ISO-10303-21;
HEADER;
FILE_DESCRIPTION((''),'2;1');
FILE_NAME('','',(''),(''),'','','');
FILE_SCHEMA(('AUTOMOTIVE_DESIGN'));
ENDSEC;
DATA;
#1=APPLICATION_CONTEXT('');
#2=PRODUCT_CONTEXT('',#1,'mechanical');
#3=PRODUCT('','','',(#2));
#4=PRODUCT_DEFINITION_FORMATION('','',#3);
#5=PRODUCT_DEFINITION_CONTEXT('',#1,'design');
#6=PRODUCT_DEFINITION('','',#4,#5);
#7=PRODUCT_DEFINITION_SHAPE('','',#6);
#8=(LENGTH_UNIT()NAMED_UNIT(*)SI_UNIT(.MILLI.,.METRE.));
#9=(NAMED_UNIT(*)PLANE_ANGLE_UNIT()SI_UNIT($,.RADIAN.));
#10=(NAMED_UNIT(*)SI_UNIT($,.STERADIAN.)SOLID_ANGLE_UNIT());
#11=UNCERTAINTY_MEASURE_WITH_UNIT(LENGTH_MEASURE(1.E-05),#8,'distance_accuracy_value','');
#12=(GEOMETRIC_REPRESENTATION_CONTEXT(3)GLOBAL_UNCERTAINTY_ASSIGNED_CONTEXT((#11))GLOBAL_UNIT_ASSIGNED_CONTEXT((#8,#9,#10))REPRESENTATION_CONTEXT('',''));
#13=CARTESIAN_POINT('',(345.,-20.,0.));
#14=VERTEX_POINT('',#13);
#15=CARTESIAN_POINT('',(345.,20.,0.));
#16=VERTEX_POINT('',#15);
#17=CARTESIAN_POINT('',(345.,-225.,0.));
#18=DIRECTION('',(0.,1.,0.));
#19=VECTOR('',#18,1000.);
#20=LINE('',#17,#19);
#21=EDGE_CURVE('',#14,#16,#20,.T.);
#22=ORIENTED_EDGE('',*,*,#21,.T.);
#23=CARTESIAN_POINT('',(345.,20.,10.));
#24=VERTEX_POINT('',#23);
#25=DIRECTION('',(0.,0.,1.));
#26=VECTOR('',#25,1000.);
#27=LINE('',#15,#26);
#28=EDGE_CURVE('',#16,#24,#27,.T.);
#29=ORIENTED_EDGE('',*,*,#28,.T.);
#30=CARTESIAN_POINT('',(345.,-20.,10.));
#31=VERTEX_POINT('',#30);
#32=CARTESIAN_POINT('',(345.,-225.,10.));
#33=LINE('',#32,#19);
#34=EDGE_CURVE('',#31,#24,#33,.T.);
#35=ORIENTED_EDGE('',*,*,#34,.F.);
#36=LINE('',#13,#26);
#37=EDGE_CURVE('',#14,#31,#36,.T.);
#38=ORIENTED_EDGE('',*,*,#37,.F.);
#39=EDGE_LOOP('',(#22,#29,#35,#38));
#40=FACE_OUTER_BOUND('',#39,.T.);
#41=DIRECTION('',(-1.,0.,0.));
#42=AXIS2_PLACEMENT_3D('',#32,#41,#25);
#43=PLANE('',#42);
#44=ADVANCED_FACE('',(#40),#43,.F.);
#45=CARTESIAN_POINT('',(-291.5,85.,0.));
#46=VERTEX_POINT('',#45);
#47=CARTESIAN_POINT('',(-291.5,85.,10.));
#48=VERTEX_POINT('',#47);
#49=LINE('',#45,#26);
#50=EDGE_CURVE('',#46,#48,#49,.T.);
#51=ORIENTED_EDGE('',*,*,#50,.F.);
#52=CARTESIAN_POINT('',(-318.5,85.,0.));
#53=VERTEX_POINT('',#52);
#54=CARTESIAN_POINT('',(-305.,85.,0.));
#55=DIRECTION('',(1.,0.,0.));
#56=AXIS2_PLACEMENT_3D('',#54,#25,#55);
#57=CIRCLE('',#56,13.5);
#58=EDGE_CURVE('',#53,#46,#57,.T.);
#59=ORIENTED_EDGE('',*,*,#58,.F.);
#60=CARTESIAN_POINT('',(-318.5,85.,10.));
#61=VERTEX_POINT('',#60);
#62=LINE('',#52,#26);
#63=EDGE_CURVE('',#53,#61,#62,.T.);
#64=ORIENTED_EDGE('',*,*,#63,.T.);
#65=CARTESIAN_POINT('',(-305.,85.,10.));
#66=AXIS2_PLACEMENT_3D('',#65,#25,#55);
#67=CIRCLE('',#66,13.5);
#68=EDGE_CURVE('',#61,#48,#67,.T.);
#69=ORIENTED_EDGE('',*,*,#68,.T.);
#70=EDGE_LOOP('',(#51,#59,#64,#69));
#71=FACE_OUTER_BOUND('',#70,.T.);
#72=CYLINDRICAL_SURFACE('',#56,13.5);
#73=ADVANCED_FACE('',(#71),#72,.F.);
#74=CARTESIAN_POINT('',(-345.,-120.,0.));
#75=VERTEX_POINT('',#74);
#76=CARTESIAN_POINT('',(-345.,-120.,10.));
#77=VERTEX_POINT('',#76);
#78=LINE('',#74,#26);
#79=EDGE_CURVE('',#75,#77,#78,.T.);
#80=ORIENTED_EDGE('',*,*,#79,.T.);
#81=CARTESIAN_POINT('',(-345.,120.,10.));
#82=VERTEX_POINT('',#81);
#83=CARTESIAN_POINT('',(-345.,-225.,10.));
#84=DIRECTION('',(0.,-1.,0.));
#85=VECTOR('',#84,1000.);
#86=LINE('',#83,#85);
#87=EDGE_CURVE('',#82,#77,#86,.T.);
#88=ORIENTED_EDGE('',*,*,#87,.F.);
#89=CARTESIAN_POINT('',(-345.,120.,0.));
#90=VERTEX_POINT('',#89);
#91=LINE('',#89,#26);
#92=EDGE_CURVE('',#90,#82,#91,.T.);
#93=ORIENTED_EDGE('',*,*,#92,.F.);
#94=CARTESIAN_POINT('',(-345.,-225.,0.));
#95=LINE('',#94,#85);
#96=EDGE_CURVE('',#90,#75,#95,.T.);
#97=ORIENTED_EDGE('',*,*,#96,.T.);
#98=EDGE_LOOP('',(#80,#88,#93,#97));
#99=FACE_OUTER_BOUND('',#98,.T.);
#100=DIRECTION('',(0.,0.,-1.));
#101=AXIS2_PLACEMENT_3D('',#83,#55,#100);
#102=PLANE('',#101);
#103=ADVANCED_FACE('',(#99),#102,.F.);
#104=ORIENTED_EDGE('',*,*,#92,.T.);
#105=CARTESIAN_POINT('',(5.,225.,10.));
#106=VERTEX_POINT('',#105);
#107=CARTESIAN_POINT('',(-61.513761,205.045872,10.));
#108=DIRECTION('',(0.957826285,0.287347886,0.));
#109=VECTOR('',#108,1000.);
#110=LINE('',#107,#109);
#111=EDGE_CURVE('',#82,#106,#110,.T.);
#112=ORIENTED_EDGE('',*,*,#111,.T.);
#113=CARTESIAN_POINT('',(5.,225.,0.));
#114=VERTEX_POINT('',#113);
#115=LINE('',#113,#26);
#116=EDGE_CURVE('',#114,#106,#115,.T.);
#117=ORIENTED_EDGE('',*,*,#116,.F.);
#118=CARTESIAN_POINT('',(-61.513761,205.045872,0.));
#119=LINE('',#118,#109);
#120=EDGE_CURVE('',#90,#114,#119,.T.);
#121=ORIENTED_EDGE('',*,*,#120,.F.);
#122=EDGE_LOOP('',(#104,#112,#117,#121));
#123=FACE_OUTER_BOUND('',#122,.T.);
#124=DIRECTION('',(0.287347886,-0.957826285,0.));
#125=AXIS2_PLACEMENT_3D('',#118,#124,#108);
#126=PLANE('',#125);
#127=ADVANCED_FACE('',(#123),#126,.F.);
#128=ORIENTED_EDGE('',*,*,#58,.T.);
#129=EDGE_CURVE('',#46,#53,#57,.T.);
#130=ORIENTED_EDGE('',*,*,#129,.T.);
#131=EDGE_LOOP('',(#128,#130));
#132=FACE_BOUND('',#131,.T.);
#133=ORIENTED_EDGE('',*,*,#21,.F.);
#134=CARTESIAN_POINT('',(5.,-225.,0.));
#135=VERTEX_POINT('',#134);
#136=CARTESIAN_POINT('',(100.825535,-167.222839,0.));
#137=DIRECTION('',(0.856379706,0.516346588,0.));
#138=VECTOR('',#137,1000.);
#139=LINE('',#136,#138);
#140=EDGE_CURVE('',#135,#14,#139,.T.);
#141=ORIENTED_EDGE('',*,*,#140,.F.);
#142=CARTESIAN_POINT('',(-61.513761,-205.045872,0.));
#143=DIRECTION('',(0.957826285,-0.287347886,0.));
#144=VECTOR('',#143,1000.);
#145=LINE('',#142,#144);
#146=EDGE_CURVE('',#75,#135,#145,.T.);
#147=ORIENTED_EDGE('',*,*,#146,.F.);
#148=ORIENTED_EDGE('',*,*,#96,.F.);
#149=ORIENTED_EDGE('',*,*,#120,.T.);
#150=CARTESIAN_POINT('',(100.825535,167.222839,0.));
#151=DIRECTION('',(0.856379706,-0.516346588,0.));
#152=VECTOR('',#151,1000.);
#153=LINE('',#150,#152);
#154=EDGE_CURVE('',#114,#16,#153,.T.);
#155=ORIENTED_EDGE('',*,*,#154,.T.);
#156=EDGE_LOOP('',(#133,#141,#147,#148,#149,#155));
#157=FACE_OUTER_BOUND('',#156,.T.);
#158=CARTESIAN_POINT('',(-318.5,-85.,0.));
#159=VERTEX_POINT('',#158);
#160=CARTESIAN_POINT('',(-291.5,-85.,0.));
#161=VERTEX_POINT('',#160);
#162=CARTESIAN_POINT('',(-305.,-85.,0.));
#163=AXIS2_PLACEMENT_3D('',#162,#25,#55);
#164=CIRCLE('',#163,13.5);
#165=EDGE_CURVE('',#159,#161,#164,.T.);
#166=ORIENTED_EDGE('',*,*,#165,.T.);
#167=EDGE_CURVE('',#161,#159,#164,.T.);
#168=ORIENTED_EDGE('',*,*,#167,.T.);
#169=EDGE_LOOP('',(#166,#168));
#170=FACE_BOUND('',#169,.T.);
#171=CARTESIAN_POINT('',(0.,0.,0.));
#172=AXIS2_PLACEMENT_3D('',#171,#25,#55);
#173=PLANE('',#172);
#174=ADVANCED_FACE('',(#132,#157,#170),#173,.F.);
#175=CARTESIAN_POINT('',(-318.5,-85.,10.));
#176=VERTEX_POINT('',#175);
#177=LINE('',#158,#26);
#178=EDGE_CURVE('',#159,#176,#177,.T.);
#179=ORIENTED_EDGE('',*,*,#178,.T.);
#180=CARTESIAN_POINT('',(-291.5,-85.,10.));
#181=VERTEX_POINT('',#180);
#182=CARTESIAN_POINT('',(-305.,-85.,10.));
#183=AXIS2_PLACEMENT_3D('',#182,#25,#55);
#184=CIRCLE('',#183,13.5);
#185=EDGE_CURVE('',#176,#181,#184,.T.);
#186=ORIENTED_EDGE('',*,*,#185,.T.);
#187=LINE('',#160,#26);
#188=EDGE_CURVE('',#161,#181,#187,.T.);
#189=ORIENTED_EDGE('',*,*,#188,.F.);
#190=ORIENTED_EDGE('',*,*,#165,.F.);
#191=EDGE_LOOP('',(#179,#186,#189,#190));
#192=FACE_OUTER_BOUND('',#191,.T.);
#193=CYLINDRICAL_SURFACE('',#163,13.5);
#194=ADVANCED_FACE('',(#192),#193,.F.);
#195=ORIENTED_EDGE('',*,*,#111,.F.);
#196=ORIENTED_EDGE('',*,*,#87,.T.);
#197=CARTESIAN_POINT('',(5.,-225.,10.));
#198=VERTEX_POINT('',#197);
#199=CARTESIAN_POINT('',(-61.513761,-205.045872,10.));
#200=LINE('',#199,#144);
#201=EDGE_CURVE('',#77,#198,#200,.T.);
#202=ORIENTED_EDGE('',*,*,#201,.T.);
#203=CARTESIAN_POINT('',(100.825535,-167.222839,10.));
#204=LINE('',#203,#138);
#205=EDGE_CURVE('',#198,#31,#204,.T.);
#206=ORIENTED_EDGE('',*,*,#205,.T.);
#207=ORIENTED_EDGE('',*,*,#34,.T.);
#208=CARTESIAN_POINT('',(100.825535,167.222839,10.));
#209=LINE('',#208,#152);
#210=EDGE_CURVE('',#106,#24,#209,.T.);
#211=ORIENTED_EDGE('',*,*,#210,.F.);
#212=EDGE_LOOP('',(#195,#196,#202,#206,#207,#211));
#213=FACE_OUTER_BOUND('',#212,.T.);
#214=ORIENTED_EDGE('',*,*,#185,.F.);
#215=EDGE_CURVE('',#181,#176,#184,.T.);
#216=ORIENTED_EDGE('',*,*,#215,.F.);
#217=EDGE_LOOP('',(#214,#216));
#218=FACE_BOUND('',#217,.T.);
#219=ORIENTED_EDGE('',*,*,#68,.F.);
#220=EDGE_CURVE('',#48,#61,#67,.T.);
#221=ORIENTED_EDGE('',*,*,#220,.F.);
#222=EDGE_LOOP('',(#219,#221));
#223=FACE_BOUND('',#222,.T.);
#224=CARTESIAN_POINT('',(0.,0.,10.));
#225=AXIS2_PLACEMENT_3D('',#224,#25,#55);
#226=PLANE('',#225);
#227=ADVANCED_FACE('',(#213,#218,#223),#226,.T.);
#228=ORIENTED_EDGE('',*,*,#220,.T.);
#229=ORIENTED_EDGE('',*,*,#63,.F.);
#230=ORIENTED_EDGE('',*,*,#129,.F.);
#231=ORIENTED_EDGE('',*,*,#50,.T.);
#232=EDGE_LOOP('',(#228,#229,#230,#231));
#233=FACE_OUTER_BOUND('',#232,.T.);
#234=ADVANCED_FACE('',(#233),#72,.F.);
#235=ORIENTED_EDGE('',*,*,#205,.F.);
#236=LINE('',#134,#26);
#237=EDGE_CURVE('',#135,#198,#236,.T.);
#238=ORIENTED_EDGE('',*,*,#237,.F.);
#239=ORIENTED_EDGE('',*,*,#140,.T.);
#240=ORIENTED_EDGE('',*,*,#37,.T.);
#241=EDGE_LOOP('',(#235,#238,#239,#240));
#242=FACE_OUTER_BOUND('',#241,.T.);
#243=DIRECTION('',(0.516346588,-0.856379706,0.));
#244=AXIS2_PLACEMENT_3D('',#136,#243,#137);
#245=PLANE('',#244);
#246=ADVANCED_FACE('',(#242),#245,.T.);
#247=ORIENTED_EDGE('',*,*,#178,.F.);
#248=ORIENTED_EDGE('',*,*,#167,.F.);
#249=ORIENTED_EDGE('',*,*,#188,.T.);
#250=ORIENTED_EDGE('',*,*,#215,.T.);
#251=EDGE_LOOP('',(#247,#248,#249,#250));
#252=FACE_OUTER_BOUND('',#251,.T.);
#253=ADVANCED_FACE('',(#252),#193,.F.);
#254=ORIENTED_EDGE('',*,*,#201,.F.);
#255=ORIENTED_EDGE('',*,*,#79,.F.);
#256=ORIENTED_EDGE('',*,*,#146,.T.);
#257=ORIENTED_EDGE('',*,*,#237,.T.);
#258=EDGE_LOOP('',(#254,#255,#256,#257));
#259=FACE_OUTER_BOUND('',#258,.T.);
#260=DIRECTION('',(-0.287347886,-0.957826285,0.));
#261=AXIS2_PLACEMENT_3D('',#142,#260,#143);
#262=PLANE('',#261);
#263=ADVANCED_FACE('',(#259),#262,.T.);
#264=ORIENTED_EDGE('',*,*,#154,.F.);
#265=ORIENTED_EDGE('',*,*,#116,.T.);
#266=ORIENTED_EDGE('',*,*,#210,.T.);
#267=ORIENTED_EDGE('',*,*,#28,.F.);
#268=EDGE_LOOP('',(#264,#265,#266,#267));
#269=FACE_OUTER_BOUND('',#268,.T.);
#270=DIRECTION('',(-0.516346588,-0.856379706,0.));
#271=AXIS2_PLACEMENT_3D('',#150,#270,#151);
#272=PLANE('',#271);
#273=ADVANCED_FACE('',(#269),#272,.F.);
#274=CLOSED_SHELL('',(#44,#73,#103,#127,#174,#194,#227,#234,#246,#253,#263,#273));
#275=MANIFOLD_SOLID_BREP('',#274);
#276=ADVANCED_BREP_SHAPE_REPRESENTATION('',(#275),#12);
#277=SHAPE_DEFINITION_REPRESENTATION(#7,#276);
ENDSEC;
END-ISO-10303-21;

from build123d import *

# Parameters (mm, degrees)
SKETCH_1_W          = 690
SKETCH_1_H          = 450
EXTRUDE_1_DEPTH     = 10
SKETCH_2_R          = 13.5
CUT_EXTRUDE_1_DEPTH = 10


with BuildPart() as part:
    # 草图1 → 凸台-拉伸1 (new body)
    with BuildSketch(Plane.XY):
        Rectangle(SKETCH_1_W, SKETCH_1_H)
    extrude(amount=EXTRUDE_1_DEPTH)

    # 草图2 → 切除-拉伸1 (cut)
    with BuildSketch(Plane.XY.offset(10)):
        Polygon((-345, 225), (-345, 120), (5, 225), align=None)
        Polygon((345, 225), (5, 225), (345, 20), align=None)
        Polygon((345, -20), (5, -225), (345, -225), align=None)
        Polygon((5, -225), (-345, -120), (-345, -225), align=None)
        with Locations((-305, -85)):
            Circle(SKETCH_2_R)
        with Locations((-305, 85)):
            Circle(SKETCH_2_R)
    extrude(amount=-CUT_EXTRUDE_1_DEPTH, mode=Mode.SUBTRACT)


solid = part.part
